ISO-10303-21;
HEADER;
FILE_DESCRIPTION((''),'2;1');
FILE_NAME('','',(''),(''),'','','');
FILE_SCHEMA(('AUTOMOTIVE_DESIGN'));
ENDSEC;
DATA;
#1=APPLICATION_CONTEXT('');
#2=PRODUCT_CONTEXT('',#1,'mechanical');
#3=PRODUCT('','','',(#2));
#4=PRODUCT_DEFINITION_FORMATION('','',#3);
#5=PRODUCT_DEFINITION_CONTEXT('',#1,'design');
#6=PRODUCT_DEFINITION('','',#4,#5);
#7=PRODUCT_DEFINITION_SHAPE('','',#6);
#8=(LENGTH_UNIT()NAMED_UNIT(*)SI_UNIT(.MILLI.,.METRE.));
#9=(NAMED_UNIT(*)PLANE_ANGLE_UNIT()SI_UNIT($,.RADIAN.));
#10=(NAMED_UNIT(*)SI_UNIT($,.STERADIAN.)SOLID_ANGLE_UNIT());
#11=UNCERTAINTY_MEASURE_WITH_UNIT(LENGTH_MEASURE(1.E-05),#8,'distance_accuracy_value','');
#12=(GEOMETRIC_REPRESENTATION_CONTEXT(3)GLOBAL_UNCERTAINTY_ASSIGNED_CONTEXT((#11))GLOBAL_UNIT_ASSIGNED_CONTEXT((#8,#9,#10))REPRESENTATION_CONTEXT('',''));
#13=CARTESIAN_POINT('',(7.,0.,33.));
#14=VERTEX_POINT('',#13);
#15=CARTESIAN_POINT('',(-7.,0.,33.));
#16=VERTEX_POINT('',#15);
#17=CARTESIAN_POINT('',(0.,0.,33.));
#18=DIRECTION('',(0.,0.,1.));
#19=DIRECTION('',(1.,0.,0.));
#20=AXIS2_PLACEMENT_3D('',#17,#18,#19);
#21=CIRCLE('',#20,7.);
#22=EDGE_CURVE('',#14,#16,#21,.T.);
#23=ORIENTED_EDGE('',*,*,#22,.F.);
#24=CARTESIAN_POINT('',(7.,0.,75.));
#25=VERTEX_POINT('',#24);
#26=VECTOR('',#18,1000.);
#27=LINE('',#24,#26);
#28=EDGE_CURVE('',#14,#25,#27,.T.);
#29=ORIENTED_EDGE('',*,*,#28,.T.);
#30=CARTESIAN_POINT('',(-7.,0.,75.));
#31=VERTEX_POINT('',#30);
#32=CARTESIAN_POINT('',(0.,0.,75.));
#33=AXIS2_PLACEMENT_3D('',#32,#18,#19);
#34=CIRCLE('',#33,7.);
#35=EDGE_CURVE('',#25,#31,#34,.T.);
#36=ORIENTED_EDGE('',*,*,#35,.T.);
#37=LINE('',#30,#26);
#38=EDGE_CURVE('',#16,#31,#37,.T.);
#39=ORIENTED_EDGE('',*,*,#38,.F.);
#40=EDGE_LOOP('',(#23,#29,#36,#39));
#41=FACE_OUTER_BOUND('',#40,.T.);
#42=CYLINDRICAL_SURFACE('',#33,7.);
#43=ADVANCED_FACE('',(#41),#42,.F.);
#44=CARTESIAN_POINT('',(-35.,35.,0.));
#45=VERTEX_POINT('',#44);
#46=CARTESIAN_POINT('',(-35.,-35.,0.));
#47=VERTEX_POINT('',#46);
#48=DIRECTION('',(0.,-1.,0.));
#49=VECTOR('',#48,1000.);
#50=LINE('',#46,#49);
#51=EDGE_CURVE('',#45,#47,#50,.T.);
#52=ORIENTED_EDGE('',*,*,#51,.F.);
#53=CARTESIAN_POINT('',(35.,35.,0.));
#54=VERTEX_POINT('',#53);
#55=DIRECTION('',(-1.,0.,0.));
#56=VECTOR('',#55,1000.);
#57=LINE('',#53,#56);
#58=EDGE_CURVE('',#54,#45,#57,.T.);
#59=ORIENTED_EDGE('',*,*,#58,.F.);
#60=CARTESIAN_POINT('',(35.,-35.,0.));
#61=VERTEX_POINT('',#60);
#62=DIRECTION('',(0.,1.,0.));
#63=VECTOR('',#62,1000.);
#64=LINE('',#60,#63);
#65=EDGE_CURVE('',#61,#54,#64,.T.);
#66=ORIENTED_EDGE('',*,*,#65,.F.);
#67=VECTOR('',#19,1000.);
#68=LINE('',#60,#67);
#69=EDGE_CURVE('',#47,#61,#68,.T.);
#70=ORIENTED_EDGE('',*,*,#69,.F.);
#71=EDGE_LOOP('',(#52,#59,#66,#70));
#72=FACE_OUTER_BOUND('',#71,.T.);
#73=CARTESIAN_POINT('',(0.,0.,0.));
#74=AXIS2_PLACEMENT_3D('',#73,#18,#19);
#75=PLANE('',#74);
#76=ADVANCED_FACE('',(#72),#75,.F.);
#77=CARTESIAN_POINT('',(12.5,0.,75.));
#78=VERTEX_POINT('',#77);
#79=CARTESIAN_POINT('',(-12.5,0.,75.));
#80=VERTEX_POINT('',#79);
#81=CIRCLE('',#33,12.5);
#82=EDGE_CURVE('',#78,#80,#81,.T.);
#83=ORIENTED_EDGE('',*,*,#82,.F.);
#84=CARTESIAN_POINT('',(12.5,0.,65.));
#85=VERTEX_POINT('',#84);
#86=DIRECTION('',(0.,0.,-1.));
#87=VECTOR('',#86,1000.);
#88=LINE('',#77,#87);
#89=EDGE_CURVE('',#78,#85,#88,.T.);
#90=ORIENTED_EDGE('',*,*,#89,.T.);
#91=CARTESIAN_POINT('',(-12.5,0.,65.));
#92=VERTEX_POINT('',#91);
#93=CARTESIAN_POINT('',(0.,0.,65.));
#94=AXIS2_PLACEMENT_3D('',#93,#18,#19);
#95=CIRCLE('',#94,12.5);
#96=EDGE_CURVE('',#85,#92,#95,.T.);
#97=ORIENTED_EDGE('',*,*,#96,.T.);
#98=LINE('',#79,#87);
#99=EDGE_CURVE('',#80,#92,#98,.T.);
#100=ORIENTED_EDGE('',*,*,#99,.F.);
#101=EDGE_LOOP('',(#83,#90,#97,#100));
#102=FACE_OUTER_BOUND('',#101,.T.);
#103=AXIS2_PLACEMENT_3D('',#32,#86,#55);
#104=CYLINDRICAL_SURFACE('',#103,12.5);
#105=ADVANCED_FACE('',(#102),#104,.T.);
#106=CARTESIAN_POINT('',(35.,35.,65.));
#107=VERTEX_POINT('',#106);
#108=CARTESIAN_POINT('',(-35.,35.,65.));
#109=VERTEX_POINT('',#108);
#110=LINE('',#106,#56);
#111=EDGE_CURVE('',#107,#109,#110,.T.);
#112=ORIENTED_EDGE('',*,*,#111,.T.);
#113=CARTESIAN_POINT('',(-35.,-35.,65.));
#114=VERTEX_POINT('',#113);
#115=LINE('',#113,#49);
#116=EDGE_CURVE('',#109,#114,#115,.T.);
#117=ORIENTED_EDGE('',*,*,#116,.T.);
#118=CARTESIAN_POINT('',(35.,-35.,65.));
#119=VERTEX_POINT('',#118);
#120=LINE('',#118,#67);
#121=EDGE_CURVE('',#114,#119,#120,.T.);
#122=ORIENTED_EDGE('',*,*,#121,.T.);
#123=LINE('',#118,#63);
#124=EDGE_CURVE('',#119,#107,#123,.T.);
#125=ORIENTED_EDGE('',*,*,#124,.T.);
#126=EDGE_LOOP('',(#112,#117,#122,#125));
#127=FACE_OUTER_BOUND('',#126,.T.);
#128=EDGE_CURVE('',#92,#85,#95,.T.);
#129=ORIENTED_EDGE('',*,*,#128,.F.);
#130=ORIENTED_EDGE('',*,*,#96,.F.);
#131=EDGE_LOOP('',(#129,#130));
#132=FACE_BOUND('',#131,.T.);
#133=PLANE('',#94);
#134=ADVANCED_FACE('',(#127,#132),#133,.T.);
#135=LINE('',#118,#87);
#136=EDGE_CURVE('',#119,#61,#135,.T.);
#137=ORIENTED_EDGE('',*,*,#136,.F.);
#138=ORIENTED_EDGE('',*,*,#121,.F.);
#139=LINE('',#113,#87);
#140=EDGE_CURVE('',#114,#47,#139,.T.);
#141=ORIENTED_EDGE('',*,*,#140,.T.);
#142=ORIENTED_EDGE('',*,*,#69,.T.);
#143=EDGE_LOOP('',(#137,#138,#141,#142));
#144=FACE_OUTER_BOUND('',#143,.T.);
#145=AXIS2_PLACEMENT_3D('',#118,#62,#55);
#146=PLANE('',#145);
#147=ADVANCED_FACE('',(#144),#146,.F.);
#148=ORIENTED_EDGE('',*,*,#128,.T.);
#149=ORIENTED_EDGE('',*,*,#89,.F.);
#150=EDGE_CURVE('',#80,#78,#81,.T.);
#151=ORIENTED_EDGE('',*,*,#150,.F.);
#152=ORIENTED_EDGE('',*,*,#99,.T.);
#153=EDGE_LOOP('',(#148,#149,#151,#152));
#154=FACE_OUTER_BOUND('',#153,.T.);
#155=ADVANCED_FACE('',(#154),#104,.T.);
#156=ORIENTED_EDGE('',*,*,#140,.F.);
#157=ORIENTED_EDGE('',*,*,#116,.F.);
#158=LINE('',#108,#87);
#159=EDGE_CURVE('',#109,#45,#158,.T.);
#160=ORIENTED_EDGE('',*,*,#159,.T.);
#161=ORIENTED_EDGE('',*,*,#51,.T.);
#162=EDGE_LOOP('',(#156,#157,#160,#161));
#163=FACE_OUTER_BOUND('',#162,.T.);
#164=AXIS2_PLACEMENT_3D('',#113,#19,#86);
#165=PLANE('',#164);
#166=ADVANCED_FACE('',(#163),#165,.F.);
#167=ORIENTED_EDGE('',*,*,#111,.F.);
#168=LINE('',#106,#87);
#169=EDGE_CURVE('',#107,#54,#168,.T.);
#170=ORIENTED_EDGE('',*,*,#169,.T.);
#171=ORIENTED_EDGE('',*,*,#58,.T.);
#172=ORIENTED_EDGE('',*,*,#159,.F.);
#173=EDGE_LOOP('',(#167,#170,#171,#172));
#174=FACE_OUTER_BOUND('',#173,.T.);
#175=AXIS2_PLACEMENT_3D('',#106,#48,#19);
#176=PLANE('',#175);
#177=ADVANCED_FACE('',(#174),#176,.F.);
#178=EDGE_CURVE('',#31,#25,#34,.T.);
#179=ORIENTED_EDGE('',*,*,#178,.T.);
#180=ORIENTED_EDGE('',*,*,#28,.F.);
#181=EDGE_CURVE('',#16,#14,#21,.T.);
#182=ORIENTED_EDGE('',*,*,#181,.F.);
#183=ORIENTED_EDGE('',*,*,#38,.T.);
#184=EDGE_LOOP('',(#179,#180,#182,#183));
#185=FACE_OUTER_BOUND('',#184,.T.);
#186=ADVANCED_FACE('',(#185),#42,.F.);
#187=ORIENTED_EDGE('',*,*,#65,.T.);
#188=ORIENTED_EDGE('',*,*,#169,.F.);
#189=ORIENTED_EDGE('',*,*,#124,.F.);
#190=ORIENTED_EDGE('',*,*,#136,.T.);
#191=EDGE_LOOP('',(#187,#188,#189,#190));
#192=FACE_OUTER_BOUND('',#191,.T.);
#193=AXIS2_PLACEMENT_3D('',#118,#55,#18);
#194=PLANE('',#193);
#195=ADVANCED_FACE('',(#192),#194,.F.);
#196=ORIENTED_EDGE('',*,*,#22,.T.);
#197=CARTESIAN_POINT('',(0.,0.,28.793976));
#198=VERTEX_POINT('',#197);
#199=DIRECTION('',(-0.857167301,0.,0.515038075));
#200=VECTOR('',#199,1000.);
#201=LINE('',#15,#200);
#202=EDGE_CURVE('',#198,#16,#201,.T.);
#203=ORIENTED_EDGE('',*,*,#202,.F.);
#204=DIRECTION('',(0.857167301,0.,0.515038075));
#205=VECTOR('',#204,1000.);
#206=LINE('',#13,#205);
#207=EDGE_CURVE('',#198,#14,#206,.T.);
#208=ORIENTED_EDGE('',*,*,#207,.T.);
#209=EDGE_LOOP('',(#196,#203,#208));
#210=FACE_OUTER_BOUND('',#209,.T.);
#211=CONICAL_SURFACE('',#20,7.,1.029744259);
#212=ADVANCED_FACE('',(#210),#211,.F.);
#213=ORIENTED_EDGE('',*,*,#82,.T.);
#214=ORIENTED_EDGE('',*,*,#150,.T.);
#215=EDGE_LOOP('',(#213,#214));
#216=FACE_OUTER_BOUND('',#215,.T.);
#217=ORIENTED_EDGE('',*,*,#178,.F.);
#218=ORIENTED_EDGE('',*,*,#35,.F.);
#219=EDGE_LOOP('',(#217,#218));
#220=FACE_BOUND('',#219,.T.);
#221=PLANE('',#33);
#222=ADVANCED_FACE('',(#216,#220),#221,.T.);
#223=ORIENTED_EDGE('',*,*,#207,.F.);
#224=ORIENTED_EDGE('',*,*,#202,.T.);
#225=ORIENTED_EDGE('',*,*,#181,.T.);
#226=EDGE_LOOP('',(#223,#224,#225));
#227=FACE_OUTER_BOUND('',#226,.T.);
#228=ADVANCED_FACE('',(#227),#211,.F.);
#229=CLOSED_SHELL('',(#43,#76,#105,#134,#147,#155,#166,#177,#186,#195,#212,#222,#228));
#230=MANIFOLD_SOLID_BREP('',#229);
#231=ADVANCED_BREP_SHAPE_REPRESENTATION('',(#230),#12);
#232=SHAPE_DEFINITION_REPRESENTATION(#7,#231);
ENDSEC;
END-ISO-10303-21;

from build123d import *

# Parameters (mm, degrees)
SKETCH1_W              = 70
SKETCH1_H              = 70
BOSS_EXTRUDE1_DEPTH    = 65
SKETCH2_R              = 12.5
BOSS_EXTRUDE2_DEPTH    = 10
M16_TAPPED_HOLE1_D     = 14
M16_TAPPED_HOLE1_DEPTH = 42
M16_TAPPED_HOLE1_TIP   = 4.206024333


with BuildPart() as part:
    # Sketch1 → Boss-Extrude1 (new body)
    with BuildSketch(Plane.XY):
        Rectangle(SKETCH1_W, SKETCH1_H)
    extrude(amount=BOSS_EXTRUDE1_DEPTH)

    # Sketch2 → Boss-Extrude2 (add)
    with BuildSketch(Plane.XY.offset(65)):
        Circle(SKETCH2_R)
    extrude(amount=BOSS_EXTRUDE2_DEPTH)

    # M16 Tapped Hole1
    with Locations(Plane.XY.offset(75)):
        with Locations((0, 0)):
            Hole(M16_TAPPED_HOLE1_D / 2, depth=M16_TAPPED_HOLE1_DEPTH)
            with Locations((0, 0, -(M16_TAPPED_HOLE1_DEPTH + M16_TAPPED_HOLE1_TIP / 2))):  # 118° drill point
                Cone(0, M16_TAPPED_HOLE1_D / 2, M16_TAPPED_HOLE1_TIP, mode=Mode.SUBTRACT)


solid = part.part
